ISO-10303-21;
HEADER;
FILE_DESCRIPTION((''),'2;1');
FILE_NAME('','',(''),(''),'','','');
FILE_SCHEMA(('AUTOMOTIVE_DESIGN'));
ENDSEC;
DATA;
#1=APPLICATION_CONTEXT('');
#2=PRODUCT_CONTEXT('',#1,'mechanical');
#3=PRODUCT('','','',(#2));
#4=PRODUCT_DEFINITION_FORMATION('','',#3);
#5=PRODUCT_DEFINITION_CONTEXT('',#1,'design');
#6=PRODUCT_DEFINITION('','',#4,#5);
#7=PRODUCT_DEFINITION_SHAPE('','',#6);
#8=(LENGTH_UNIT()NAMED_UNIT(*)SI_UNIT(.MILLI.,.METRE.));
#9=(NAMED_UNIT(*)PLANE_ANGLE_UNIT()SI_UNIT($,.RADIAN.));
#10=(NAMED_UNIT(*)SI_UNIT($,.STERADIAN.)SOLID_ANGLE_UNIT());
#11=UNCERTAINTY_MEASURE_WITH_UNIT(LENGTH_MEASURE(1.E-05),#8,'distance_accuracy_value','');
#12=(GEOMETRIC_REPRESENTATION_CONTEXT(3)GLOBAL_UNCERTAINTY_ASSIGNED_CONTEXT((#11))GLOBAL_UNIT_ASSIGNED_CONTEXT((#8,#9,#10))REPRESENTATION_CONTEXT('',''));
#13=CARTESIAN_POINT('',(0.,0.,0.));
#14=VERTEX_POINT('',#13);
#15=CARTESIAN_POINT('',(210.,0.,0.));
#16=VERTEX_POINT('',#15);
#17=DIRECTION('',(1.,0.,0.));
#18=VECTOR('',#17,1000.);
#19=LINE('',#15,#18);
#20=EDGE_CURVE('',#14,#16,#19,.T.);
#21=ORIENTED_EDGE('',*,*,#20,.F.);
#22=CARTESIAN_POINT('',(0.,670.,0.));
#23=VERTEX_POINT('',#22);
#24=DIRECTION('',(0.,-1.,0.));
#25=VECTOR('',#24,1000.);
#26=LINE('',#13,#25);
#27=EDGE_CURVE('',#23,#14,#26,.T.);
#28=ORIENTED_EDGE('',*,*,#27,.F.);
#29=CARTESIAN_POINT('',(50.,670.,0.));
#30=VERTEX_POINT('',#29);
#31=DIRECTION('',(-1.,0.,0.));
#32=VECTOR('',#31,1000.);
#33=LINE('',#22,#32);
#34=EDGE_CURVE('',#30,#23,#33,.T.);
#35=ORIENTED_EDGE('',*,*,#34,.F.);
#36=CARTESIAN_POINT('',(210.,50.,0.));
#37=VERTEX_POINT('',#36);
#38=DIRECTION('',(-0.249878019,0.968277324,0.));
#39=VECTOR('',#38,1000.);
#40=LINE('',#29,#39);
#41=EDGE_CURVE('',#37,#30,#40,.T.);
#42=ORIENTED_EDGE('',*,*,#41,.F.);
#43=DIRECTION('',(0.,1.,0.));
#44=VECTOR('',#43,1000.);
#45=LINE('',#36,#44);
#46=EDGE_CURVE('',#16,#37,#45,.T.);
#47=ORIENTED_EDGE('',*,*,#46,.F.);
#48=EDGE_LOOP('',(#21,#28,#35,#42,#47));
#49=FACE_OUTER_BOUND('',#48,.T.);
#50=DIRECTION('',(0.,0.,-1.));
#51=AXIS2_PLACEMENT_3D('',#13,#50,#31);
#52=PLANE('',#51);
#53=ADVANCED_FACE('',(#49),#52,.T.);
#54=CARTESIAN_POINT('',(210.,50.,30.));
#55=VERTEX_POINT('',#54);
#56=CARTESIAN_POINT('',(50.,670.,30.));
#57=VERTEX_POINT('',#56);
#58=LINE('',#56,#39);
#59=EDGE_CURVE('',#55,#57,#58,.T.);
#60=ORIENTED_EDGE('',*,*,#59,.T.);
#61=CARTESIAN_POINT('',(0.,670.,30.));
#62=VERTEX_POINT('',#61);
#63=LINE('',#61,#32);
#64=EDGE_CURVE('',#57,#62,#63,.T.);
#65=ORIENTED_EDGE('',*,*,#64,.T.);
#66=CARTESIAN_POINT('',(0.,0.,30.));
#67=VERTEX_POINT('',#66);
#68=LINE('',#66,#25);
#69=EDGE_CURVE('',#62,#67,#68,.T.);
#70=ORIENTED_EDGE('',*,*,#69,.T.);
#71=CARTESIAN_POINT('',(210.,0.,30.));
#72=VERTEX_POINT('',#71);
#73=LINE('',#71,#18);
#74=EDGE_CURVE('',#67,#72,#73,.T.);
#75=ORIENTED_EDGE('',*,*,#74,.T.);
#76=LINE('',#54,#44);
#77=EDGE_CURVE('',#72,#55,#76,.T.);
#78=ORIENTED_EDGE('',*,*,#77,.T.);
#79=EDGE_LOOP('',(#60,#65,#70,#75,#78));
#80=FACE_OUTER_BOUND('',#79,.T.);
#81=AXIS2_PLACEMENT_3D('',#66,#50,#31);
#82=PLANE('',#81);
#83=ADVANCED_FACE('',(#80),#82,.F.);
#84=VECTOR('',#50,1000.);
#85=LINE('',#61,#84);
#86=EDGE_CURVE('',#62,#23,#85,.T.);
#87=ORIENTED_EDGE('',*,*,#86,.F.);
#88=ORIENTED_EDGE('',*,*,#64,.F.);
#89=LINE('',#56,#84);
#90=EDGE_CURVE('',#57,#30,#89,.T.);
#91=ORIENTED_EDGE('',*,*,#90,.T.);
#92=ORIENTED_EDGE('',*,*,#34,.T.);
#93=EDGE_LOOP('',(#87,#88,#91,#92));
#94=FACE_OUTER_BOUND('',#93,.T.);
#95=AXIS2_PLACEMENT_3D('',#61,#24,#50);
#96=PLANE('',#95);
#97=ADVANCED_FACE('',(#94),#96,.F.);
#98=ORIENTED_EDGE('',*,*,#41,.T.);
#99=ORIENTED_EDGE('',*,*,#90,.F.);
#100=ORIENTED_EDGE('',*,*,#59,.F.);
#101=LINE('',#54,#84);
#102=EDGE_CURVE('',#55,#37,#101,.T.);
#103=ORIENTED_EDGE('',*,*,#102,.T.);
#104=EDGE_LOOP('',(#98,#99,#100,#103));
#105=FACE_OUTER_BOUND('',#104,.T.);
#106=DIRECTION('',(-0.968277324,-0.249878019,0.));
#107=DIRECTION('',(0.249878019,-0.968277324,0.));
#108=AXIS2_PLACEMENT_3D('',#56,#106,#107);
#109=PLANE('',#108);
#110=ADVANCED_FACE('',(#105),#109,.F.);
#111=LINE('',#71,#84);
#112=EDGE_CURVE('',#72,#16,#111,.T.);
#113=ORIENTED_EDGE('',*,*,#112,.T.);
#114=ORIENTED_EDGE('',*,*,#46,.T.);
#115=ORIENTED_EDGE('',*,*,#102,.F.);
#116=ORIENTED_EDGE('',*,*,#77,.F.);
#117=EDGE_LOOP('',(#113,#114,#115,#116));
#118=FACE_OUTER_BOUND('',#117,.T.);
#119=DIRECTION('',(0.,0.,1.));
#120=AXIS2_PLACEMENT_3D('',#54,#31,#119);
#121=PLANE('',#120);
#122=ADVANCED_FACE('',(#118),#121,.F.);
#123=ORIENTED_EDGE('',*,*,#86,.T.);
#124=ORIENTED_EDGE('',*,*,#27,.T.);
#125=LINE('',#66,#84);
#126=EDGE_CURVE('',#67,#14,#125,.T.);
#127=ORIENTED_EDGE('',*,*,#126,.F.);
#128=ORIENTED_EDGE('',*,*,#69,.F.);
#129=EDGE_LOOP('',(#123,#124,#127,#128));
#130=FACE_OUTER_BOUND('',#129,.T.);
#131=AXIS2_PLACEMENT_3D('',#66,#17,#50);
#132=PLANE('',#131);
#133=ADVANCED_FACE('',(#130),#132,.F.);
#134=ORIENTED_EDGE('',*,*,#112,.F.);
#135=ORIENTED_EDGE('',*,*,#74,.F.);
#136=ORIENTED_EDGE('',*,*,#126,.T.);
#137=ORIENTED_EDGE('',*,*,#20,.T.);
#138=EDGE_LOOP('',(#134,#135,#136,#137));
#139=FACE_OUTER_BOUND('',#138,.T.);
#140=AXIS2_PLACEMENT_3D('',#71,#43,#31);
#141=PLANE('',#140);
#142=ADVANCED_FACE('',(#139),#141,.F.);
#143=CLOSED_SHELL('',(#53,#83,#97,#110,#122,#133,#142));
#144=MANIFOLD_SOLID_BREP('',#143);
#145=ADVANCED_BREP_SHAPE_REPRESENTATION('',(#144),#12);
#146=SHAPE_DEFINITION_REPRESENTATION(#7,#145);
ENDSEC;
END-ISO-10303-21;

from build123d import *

# Parameters (mm, degrees)
EXTRUDE_1_DEPTH = 30


with BuildPart() as part:
    # 草图1 → 凸台-拉伸1 (new body)
    with BuildSketch(Plane.XY):
        Polygon((0, 0), (0, 670), (50, 670), (210, 50), (210, 0), align=None)
    extrude(amount=EXTRUDE_1_DEPTH)


solid = part.part
